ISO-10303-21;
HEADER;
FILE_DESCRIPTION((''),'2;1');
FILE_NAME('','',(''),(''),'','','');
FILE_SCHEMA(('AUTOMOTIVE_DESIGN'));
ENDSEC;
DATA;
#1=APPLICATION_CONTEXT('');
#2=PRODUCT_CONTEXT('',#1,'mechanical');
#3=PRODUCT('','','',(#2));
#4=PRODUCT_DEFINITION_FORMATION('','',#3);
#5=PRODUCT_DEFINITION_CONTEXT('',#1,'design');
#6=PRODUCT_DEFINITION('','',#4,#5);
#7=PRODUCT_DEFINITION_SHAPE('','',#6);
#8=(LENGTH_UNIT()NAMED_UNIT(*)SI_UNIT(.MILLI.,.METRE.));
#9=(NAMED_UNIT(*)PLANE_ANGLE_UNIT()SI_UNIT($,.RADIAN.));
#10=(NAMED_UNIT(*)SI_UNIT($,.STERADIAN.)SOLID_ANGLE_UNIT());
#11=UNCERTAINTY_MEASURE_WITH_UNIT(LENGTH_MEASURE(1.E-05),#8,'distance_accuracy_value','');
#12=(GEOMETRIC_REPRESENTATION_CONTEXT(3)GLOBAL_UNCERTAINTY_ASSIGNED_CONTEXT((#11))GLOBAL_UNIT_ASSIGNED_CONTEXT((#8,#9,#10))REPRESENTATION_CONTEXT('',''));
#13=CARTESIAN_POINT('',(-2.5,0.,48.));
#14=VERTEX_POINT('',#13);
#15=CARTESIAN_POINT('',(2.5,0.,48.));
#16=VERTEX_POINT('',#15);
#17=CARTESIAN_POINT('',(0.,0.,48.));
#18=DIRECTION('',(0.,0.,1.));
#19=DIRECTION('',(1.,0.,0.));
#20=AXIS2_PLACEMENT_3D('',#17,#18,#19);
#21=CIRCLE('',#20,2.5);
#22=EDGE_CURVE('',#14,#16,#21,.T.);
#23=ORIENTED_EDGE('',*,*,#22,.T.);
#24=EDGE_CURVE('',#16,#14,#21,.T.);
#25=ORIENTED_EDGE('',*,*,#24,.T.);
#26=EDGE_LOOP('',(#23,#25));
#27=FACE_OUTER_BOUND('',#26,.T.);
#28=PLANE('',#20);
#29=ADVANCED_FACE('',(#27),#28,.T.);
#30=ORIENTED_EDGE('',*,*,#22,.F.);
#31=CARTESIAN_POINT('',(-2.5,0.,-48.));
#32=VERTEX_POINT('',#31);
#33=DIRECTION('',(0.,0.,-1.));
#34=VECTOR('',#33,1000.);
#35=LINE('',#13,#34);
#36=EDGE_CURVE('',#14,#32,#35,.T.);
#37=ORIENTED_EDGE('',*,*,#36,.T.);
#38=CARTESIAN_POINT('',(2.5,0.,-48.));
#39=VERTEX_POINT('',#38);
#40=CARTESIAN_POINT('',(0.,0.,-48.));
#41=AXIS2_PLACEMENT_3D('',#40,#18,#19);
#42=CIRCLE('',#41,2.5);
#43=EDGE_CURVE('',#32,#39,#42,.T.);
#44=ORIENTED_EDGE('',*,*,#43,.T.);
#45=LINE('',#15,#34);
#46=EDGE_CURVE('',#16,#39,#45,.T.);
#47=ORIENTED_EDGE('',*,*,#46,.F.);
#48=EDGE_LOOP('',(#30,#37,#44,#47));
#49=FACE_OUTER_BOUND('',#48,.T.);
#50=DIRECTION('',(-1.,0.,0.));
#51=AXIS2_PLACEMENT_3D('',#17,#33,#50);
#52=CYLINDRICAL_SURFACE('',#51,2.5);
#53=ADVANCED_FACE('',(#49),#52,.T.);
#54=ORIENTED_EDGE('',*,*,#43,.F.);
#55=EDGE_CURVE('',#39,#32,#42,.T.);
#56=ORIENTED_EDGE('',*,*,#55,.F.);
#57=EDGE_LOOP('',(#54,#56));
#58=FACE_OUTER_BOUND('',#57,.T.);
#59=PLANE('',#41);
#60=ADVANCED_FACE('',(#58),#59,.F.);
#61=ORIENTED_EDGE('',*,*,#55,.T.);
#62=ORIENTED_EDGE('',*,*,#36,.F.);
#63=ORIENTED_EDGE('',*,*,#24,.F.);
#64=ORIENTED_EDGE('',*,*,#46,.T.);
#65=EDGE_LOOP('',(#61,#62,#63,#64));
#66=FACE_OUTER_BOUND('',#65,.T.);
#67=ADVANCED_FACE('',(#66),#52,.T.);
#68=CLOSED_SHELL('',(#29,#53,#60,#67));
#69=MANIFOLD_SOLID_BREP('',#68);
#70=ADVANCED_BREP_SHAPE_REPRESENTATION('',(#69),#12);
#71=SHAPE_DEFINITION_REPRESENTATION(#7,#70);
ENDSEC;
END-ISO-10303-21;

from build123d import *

# Parameters (mm, degrees)
ROD_PROFILE_5_R = 2.5
ROD_5X96_DEPTH  = 48


with BuildPart() as part:
    # Rod Profile Ø5 → Rod Ø5x96 (new, symmetric)
    with BuildSketch(Plane.XY):
        Circle(ROD_PROFILE_5_R)
    extrude(amount=ROD_5X96_DEPTH, both=True)


solid = part.part
